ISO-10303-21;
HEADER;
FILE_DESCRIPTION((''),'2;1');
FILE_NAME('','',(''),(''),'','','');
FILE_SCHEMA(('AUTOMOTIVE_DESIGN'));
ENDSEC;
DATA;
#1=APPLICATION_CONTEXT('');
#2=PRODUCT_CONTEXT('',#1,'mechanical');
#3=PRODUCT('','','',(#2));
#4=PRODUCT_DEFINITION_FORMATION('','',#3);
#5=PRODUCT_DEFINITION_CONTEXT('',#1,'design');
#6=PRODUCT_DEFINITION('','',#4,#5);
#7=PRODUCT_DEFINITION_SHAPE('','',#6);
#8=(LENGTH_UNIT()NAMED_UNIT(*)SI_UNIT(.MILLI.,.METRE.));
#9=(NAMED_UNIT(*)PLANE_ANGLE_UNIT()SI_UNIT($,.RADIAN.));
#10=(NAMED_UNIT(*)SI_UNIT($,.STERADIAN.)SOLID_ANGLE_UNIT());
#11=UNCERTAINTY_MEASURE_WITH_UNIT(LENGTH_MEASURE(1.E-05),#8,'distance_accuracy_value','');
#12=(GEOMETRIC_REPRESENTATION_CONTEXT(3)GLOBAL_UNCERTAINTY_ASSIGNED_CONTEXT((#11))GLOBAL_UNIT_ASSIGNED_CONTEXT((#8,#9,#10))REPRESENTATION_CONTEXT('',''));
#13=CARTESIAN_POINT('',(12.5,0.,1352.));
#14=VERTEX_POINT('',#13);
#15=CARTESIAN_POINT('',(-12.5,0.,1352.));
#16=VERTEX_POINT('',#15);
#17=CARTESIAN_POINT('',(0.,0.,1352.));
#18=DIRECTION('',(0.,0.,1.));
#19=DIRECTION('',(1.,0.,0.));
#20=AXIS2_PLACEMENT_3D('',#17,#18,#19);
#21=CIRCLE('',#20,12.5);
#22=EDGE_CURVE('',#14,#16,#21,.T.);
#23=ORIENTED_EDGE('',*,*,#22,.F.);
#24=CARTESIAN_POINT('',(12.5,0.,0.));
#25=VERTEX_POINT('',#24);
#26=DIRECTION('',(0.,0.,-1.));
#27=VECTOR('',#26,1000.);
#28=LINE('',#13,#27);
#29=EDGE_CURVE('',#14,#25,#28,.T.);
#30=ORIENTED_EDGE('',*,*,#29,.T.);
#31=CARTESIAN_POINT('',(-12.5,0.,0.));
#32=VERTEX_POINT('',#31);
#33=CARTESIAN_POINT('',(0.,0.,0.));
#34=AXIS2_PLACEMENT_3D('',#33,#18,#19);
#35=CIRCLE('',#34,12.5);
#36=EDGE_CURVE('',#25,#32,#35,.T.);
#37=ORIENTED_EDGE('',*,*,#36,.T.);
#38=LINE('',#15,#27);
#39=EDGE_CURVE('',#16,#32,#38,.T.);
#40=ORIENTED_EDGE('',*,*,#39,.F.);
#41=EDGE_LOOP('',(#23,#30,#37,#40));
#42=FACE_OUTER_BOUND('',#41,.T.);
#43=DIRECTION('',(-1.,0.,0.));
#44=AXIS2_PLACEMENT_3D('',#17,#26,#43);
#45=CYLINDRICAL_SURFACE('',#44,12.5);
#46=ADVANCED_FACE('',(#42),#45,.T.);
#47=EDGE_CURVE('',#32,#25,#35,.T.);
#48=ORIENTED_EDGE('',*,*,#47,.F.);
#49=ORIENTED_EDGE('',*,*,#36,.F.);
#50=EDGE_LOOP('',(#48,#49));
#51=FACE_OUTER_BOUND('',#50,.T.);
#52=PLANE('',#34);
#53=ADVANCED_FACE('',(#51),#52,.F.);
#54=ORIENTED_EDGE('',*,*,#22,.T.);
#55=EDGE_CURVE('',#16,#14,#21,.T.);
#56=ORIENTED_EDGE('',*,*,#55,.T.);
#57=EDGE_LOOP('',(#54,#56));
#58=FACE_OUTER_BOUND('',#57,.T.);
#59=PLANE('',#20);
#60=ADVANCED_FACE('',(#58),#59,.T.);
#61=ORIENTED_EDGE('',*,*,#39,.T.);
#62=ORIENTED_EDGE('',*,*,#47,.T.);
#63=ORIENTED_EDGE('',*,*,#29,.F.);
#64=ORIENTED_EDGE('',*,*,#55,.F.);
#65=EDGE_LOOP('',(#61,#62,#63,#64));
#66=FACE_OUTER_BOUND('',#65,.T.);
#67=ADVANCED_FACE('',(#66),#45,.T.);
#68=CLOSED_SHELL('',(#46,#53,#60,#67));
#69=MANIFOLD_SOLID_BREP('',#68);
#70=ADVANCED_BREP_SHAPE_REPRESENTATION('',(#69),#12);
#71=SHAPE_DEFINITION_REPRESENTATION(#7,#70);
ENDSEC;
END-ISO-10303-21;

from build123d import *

# Parameters (mm, degrees)
SKETCH_1_R      = 12.5
EXTRUDE_1_DEPTH = 1352


with BuildPart() as part:
    # 草图1 → 凸台-拉伸1 (new body)
    with BuildSketch(Plane.XY):
        Circle(SKETCH_1_R)
    extrude(amount=EXTRUDE_1_DEPTH)


solid = part.part
